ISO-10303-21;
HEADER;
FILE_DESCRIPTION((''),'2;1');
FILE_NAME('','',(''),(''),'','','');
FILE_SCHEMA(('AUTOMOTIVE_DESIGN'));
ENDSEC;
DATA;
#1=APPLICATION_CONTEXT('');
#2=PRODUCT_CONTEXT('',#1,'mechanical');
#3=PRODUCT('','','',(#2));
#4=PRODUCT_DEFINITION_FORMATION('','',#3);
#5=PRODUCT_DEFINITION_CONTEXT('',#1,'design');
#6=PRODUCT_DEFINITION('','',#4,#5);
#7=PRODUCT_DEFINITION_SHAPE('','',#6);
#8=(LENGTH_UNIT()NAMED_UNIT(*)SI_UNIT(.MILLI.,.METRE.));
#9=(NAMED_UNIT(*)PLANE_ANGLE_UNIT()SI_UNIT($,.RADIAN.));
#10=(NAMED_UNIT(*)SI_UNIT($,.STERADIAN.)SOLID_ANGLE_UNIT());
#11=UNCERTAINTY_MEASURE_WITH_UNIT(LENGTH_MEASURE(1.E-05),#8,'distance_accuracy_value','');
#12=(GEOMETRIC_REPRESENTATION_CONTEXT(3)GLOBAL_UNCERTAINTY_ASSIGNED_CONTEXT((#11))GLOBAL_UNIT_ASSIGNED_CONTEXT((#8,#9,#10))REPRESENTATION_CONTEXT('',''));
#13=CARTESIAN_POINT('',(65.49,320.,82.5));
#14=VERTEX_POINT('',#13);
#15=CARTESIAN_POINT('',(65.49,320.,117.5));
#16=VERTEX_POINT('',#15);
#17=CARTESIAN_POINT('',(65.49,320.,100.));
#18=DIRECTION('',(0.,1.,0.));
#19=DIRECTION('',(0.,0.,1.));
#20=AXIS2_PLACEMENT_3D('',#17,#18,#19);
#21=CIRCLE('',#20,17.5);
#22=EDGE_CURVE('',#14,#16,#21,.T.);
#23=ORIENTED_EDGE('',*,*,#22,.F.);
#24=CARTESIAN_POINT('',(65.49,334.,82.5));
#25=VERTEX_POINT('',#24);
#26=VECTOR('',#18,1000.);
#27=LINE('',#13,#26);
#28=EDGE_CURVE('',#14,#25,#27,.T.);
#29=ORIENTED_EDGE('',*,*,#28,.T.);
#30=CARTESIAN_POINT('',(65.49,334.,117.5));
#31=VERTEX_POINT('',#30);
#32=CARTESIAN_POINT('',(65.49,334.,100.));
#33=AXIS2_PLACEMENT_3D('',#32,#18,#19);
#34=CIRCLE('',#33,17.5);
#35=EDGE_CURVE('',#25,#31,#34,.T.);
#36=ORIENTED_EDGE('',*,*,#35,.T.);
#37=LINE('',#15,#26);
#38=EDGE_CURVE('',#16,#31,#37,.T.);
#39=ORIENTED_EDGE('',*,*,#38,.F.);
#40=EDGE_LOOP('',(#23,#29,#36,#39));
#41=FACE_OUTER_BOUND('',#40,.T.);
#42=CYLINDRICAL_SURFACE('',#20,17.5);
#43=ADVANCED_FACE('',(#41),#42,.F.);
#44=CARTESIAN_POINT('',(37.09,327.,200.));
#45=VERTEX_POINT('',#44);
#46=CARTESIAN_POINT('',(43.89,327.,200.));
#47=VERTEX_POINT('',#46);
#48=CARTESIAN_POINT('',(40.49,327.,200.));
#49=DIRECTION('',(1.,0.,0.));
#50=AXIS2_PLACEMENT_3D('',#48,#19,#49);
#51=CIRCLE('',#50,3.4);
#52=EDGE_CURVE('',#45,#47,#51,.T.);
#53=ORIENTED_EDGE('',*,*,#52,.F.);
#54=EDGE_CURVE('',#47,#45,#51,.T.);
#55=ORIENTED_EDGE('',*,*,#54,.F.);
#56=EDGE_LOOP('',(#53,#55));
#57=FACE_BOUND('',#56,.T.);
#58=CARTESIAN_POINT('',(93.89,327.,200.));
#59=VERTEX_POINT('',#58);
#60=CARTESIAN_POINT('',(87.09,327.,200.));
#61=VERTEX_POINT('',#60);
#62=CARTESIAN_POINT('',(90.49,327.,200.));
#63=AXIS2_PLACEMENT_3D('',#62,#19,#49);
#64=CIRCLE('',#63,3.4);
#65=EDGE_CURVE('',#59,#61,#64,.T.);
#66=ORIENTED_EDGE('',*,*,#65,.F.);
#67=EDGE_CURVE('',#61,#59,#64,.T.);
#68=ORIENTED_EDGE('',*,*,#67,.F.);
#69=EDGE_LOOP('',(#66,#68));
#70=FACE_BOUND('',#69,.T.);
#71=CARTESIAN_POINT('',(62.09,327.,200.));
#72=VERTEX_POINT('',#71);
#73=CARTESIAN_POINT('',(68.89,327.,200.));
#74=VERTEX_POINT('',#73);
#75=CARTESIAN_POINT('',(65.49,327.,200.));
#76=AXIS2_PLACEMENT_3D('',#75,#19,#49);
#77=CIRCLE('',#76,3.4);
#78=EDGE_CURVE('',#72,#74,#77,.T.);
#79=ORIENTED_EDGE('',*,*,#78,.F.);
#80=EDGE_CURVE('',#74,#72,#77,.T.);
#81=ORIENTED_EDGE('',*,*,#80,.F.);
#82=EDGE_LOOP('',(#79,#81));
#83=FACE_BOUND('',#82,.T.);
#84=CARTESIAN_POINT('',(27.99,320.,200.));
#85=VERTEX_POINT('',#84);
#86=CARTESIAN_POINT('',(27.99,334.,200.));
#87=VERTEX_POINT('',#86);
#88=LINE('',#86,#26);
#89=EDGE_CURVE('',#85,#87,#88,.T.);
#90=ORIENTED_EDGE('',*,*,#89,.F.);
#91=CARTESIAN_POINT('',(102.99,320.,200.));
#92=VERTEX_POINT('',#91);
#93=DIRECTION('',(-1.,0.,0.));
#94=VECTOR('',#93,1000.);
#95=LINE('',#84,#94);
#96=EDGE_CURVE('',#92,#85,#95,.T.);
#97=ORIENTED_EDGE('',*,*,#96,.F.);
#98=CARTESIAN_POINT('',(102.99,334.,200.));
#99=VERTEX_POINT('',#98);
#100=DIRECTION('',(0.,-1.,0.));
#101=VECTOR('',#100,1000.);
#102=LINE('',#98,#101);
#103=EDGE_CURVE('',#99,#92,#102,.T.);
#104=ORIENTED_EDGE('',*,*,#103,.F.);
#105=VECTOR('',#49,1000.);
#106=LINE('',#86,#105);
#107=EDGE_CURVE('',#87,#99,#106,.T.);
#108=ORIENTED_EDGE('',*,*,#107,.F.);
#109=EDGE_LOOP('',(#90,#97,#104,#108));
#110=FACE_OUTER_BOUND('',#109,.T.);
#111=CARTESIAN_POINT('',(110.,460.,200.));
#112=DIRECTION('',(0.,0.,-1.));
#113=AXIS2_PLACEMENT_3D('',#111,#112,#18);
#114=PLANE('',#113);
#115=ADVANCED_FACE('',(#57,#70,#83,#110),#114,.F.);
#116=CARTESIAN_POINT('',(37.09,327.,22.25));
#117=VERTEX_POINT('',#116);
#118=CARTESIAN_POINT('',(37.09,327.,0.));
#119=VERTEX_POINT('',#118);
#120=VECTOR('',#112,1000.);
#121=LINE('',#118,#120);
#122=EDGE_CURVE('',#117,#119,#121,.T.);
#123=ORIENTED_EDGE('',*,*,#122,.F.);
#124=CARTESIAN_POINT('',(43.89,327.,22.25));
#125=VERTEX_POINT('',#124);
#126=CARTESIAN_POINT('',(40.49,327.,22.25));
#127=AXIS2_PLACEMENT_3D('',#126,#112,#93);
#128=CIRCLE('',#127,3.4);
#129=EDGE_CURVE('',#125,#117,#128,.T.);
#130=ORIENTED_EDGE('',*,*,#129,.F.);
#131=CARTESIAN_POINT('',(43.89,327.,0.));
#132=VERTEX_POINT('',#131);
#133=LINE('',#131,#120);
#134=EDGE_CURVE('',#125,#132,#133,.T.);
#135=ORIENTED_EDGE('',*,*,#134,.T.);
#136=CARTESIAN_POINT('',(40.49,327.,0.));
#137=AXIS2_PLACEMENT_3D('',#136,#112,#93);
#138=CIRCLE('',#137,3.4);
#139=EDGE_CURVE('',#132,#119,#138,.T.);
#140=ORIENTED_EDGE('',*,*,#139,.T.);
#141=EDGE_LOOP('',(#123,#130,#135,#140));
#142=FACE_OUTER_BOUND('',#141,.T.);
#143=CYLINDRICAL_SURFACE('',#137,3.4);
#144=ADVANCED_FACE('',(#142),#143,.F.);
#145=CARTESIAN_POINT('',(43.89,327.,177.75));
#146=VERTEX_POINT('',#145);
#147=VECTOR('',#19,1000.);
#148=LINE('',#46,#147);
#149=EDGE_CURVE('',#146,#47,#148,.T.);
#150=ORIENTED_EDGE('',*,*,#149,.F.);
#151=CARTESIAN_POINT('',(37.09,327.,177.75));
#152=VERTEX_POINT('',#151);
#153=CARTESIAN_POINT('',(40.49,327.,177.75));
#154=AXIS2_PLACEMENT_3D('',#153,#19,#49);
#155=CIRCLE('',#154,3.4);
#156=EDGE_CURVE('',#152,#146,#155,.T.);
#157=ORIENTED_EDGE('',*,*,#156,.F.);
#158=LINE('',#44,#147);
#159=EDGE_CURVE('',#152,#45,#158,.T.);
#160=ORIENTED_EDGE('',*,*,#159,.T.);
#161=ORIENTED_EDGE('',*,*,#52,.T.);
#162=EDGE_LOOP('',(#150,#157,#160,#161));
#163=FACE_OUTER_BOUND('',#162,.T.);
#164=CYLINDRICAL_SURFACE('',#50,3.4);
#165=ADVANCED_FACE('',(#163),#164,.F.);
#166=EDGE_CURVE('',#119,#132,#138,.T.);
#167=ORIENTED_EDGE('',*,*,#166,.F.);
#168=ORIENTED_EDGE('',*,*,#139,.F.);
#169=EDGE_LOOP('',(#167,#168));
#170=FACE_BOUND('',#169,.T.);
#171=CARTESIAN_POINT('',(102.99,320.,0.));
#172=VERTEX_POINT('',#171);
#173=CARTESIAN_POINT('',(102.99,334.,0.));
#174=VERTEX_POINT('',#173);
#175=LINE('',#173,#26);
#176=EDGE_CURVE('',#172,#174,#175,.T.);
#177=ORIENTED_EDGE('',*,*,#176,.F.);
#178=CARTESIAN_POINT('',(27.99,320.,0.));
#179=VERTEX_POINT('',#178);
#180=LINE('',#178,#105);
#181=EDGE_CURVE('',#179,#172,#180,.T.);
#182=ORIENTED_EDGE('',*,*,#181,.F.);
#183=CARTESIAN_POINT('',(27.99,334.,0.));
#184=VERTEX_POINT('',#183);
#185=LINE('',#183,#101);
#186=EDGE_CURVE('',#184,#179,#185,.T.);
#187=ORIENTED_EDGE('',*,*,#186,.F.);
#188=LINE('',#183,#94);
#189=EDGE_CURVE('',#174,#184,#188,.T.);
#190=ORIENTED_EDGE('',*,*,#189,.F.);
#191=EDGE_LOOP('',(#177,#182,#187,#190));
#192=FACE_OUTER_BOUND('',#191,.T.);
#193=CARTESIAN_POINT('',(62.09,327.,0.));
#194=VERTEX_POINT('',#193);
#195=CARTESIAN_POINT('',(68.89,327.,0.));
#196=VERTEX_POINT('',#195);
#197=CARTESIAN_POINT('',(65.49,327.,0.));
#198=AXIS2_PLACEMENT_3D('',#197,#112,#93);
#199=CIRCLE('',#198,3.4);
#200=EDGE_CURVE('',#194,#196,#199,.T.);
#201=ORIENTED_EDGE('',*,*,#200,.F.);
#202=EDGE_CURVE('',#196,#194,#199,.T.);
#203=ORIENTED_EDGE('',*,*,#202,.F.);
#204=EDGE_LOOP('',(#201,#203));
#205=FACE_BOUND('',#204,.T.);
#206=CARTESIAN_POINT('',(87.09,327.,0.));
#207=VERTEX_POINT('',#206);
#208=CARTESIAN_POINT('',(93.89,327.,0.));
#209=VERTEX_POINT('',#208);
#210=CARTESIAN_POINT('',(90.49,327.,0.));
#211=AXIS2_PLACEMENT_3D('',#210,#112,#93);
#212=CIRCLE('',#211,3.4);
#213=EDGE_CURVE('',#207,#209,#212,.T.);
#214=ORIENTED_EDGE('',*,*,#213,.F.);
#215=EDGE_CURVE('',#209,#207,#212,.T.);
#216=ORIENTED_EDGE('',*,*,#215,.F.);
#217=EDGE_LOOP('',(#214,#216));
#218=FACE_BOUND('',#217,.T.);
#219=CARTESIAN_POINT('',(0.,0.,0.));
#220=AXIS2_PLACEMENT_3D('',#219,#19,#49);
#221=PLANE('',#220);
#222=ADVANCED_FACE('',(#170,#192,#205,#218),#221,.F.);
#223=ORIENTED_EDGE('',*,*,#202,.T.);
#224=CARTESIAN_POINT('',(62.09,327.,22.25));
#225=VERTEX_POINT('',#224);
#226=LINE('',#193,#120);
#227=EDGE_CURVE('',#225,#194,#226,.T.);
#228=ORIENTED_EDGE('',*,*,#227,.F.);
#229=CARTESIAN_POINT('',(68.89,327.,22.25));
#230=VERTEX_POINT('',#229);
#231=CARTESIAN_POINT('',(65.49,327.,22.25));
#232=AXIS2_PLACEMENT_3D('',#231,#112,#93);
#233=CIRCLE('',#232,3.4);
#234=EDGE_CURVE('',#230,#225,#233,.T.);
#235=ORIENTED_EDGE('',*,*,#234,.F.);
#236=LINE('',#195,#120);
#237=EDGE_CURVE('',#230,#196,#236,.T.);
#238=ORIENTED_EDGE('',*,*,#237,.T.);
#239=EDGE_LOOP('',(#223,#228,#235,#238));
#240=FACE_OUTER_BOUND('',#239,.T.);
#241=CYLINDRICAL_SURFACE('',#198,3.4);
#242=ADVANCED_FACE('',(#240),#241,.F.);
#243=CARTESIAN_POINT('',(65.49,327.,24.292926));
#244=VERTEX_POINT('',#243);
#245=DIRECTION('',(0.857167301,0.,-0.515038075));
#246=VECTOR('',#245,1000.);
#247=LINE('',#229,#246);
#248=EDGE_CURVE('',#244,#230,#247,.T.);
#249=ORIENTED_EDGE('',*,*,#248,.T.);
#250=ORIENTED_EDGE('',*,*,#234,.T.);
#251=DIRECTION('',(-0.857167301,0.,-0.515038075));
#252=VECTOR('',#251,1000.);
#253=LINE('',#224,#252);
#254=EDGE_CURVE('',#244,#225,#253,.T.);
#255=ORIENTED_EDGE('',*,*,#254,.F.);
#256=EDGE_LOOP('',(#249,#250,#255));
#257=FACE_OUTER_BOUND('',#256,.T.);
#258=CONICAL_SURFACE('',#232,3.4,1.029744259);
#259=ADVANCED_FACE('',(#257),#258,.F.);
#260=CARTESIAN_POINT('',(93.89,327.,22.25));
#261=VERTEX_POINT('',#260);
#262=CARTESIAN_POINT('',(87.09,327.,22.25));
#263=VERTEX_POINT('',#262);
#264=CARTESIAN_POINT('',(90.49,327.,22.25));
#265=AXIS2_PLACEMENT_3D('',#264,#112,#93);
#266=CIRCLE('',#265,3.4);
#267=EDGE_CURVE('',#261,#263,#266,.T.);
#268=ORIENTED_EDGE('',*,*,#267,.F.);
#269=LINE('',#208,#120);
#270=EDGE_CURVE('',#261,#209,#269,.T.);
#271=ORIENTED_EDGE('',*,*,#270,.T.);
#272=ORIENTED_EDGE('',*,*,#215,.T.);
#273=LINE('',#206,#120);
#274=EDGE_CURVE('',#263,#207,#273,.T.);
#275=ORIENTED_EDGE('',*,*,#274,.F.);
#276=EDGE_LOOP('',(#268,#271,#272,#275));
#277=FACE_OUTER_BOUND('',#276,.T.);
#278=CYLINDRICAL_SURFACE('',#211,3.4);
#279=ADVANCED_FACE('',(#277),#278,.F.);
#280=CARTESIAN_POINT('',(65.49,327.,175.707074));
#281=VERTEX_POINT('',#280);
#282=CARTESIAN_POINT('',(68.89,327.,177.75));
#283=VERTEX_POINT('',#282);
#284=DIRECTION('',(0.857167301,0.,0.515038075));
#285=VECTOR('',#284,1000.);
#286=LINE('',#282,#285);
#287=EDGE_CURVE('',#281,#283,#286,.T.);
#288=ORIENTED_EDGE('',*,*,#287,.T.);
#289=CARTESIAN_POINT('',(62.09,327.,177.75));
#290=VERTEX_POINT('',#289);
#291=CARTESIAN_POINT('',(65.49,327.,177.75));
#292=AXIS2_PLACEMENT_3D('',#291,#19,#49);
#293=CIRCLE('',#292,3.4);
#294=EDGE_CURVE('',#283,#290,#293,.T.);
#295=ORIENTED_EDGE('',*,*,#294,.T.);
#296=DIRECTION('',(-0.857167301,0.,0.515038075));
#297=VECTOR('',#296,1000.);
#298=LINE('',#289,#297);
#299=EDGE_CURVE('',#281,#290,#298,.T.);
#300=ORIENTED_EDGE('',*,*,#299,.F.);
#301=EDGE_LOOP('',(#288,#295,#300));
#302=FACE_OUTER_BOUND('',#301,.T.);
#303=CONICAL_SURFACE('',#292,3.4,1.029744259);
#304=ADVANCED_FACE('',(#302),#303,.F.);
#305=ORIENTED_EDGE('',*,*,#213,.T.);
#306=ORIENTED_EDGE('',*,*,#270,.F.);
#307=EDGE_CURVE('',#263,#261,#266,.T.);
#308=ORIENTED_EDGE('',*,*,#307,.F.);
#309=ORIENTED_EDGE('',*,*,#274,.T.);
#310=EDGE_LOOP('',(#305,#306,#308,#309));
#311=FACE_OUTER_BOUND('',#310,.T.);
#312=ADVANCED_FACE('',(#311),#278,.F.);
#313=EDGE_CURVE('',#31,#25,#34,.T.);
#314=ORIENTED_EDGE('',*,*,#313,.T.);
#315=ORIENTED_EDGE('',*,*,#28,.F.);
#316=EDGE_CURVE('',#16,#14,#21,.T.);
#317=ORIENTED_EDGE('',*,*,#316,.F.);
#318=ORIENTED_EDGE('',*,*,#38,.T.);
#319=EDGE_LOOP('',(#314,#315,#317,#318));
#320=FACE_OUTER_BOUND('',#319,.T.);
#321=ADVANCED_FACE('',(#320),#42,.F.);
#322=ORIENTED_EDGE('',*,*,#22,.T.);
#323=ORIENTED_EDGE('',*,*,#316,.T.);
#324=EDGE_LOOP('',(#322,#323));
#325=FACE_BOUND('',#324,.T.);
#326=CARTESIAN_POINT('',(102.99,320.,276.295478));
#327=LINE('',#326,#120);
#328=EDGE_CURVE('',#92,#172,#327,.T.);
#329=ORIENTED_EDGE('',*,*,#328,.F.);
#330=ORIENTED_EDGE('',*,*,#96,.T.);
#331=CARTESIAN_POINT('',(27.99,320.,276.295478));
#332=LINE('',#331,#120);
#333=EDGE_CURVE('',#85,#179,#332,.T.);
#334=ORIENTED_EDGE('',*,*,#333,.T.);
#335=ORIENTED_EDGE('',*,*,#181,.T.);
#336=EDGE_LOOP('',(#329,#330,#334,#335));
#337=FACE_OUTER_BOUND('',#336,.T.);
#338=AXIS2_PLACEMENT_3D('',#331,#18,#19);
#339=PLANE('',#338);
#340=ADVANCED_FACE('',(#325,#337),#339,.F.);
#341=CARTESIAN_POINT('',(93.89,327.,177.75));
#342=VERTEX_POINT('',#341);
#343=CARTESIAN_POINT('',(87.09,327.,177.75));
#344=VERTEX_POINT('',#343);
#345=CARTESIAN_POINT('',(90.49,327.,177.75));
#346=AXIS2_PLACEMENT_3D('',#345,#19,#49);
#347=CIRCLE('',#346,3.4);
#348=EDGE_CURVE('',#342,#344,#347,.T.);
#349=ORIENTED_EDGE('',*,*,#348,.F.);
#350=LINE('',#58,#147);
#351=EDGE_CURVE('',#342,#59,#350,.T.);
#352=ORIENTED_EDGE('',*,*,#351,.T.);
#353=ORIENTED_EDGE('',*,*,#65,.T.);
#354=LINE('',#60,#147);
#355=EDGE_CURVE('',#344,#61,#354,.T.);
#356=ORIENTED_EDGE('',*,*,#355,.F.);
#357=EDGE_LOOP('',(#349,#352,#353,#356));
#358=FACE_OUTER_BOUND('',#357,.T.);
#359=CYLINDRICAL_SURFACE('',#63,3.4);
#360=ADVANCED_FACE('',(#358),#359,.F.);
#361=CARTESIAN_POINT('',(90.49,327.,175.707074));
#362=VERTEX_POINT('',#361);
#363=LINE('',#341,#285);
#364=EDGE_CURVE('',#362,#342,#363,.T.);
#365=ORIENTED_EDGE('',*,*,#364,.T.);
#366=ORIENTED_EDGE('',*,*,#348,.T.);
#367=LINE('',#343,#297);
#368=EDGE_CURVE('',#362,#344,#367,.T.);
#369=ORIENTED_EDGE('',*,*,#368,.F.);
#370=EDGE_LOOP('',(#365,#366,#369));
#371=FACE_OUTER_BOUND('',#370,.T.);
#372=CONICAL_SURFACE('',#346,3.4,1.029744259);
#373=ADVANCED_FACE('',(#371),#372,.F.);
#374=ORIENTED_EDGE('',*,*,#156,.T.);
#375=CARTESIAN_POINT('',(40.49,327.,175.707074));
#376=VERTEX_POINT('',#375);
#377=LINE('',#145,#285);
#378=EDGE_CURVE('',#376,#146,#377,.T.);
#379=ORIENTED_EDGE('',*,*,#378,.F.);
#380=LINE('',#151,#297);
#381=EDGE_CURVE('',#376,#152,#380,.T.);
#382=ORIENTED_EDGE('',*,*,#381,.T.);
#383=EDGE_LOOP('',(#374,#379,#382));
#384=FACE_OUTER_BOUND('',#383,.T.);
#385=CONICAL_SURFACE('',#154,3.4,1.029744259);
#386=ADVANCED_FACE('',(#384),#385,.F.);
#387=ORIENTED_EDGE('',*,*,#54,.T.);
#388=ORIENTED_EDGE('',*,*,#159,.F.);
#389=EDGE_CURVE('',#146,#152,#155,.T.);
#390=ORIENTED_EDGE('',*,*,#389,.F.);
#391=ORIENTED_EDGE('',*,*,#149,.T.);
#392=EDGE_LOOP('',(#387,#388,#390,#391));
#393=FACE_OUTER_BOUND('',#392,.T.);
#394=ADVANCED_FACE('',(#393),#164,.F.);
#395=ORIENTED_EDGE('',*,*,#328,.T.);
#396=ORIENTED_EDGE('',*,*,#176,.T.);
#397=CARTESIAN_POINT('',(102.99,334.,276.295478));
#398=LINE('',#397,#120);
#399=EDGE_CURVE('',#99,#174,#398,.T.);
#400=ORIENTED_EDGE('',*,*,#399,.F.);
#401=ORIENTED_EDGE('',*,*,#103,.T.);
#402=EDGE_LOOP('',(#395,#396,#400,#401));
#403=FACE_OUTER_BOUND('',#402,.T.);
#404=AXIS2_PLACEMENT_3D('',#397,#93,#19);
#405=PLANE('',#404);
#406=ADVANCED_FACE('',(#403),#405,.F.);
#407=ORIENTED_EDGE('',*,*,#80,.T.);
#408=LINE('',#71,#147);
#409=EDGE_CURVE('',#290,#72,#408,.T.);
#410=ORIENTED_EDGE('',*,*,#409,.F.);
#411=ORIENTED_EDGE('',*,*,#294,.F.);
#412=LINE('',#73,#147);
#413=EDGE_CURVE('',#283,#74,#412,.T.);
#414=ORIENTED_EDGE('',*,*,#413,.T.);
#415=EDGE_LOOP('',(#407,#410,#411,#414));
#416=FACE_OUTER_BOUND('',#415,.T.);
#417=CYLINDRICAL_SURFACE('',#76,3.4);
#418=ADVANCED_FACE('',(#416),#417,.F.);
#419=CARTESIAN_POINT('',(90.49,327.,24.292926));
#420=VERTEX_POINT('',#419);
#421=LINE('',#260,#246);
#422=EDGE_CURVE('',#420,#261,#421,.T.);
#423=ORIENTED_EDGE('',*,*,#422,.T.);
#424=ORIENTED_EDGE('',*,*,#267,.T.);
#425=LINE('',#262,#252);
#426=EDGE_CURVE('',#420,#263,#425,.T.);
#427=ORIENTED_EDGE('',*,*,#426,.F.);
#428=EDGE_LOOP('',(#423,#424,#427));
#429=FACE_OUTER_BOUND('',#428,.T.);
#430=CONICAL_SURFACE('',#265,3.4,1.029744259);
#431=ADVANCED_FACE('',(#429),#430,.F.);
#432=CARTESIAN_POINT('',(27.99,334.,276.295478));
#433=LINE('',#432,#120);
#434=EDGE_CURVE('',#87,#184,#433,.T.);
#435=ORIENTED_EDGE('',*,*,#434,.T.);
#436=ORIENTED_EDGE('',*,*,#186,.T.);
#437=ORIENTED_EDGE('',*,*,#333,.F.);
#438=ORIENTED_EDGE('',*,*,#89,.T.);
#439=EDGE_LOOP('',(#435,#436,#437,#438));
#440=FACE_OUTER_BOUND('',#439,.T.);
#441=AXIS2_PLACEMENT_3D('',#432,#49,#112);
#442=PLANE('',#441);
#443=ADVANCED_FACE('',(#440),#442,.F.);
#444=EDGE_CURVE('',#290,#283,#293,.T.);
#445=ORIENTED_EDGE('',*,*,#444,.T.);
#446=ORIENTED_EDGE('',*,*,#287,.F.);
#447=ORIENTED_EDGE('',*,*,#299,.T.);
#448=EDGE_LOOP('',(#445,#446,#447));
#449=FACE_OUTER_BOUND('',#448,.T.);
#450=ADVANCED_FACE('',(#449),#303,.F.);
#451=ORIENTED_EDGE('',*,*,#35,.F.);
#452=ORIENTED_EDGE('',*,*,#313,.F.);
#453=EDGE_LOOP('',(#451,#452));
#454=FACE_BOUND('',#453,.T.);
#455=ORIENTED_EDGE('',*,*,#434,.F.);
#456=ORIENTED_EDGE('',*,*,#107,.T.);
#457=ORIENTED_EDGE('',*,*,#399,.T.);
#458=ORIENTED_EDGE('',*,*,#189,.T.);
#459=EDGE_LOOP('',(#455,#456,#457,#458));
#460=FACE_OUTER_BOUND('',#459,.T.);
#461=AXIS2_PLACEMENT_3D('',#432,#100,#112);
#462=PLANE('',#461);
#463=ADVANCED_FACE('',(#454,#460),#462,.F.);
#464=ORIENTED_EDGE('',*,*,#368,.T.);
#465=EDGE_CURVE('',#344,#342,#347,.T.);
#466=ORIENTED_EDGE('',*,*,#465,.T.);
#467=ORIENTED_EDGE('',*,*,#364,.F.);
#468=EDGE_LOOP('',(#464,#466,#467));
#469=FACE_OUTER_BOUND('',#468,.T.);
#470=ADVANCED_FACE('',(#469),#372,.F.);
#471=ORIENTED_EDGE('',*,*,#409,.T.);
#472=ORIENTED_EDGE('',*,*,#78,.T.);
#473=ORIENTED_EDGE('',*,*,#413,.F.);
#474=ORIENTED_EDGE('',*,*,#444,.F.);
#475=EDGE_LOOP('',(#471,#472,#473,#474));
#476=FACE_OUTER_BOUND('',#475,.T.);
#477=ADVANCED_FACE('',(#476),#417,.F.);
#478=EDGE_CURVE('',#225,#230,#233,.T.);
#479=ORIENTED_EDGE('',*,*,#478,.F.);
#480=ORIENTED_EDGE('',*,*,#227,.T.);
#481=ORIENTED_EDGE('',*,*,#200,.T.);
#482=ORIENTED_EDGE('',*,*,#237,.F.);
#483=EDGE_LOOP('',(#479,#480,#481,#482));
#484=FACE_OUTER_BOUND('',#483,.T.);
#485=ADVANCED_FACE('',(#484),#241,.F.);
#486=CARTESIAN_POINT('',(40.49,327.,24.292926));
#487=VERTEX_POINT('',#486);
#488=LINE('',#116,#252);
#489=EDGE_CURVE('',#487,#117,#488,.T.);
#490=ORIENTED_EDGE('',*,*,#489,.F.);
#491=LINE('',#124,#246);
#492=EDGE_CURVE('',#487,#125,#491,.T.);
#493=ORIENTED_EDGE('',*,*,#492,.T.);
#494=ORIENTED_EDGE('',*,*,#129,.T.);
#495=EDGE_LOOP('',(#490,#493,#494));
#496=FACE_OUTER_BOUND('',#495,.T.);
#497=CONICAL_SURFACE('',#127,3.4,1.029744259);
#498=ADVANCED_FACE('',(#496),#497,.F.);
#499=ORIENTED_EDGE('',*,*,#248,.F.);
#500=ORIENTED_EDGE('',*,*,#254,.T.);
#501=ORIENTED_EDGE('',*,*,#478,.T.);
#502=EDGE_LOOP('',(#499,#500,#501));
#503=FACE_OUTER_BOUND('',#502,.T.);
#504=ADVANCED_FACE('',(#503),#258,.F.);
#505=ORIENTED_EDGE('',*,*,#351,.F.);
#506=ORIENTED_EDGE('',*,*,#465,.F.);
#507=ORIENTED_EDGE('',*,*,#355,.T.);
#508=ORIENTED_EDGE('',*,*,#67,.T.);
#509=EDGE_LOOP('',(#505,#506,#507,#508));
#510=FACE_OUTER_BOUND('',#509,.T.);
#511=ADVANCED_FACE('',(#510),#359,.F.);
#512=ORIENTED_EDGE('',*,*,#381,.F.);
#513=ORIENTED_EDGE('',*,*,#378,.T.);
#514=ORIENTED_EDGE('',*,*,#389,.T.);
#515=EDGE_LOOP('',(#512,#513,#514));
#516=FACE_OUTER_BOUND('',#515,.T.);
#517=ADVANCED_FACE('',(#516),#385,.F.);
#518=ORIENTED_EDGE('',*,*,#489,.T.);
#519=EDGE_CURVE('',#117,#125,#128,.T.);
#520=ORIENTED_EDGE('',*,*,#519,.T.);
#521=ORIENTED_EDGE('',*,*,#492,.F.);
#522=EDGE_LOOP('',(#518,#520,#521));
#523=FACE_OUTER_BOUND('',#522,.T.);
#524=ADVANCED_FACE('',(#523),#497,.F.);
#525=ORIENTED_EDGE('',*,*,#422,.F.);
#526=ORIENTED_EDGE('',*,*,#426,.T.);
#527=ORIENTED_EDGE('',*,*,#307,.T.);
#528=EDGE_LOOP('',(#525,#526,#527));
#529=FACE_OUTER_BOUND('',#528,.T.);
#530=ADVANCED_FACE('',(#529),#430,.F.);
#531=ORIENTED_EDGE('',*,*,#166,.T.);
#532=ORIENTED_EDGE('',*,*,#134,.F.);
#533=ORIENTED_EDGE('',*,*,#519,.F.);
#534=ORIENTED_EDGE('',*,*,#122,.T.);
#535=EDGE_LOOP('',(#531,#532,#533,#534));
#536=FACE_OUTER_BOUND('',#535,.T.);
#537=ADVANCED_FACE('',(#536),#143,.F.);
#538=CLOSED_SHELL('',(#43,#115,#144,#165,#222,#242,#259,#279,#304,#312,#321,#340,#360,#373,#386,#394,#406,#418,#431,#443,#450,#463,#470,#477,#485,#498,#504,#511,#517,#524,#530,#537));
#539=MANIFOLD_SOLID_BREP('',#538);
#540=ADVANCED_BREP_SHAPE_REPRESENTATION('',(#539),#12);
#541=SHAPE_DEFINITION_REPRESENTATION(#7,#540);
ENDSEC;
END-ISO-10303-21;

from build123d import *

# Parameters (mm, degrees)
SKETCH1_W             = 75
SKETCH1_H             = 14
BOSS_EXTRUDE1_DEPTH   = 200
SKETCH2_R             = 17.5
CUT_EXTRUDE1_DEPTH    = 226.39507559
M8_TAPPED_HOLE2_D     = 6.8
M8_TAPPED_HOLE2_DEPTH = 22.25
M8_TAPPED_HOLE2_TIP   = 2.042926105
M8_TAPPED_HOLE3_D     = 6.8
M8_TAPPED_HOLE3_DEPTH = 22.25
M8_TAPPED_HOLE3_TIP   = 2.042926105


with BuildPart() as part:
    # Sketch1 → Boss-Extrude1 (new body)
    with BuildSketch(Plane.XY):
        with Locations((65.49, 327)):
            Rectangle(SKETCH1_W, SKETCH1_H)
    extrude(amount=BOSS_EXTRUDE1_DEPTH)

    # Sketch2 → Cut-Extrude1 (cut, through all)
    with BuildSketch(Plane(origin=(0, 334, 0), x_dir=(1, 0, 0), z_dir=(0, 1, 0))):
        with Locations(Location((65.49, -100, 0), (0, 0, 270))):
            Circle(SKETCH2_R)
    extrude(amount=-CUT_EXTRUDE1_DEPTH, mode=Mode.SUBTRACT)

    # M8 Tapped Hole2
    with Locations(Plane.XY.offset(200)):
        with Locations((65.49, 327), (40.49, 327), (90.49, 327)):
            Hole(M8_TAPPED_HOLE2_D / 2, depth=M8_TAPPED_HOLE2_DEPTH)
            with Locations((0, 0, -(M8_TAPPED_HOLE2_DEPTH + M8_TAPPED_HOLE2_TIP / 2))):  # 118° drill point
                Cone(0, M8_TAPPED_HOLE2_D / 2, M8_TAPPED_HOLE2_TIP, mode=Mode.SUBTRACT)

    # M8 Tapped Hole3
    with Locations(Plane(origin=(0, 0, 0), x_dir=(-1, 0, 0), z_dir=(0, 0, -1))):
        with Locations((-90.49, 327), (-65.49, 327), (-40.49, 327)):
            Hole(M8_TAPPED_HOLE3_D / 2, depth=M8_TAPPED_HOLE3_DEPTH)
            with Locations((0, 0, -(M8_TAPPED_HOLE3_DEPTH + M8_TAPPED_HOLE3_TIP / 2))):  # 118° drill point
                Cone(0, M8_TAPPED_HOLE3_D / 2, M8_TAPPED_HOLE3_TIP, mode=Mode.SUBTRACT)


solid = part.part
